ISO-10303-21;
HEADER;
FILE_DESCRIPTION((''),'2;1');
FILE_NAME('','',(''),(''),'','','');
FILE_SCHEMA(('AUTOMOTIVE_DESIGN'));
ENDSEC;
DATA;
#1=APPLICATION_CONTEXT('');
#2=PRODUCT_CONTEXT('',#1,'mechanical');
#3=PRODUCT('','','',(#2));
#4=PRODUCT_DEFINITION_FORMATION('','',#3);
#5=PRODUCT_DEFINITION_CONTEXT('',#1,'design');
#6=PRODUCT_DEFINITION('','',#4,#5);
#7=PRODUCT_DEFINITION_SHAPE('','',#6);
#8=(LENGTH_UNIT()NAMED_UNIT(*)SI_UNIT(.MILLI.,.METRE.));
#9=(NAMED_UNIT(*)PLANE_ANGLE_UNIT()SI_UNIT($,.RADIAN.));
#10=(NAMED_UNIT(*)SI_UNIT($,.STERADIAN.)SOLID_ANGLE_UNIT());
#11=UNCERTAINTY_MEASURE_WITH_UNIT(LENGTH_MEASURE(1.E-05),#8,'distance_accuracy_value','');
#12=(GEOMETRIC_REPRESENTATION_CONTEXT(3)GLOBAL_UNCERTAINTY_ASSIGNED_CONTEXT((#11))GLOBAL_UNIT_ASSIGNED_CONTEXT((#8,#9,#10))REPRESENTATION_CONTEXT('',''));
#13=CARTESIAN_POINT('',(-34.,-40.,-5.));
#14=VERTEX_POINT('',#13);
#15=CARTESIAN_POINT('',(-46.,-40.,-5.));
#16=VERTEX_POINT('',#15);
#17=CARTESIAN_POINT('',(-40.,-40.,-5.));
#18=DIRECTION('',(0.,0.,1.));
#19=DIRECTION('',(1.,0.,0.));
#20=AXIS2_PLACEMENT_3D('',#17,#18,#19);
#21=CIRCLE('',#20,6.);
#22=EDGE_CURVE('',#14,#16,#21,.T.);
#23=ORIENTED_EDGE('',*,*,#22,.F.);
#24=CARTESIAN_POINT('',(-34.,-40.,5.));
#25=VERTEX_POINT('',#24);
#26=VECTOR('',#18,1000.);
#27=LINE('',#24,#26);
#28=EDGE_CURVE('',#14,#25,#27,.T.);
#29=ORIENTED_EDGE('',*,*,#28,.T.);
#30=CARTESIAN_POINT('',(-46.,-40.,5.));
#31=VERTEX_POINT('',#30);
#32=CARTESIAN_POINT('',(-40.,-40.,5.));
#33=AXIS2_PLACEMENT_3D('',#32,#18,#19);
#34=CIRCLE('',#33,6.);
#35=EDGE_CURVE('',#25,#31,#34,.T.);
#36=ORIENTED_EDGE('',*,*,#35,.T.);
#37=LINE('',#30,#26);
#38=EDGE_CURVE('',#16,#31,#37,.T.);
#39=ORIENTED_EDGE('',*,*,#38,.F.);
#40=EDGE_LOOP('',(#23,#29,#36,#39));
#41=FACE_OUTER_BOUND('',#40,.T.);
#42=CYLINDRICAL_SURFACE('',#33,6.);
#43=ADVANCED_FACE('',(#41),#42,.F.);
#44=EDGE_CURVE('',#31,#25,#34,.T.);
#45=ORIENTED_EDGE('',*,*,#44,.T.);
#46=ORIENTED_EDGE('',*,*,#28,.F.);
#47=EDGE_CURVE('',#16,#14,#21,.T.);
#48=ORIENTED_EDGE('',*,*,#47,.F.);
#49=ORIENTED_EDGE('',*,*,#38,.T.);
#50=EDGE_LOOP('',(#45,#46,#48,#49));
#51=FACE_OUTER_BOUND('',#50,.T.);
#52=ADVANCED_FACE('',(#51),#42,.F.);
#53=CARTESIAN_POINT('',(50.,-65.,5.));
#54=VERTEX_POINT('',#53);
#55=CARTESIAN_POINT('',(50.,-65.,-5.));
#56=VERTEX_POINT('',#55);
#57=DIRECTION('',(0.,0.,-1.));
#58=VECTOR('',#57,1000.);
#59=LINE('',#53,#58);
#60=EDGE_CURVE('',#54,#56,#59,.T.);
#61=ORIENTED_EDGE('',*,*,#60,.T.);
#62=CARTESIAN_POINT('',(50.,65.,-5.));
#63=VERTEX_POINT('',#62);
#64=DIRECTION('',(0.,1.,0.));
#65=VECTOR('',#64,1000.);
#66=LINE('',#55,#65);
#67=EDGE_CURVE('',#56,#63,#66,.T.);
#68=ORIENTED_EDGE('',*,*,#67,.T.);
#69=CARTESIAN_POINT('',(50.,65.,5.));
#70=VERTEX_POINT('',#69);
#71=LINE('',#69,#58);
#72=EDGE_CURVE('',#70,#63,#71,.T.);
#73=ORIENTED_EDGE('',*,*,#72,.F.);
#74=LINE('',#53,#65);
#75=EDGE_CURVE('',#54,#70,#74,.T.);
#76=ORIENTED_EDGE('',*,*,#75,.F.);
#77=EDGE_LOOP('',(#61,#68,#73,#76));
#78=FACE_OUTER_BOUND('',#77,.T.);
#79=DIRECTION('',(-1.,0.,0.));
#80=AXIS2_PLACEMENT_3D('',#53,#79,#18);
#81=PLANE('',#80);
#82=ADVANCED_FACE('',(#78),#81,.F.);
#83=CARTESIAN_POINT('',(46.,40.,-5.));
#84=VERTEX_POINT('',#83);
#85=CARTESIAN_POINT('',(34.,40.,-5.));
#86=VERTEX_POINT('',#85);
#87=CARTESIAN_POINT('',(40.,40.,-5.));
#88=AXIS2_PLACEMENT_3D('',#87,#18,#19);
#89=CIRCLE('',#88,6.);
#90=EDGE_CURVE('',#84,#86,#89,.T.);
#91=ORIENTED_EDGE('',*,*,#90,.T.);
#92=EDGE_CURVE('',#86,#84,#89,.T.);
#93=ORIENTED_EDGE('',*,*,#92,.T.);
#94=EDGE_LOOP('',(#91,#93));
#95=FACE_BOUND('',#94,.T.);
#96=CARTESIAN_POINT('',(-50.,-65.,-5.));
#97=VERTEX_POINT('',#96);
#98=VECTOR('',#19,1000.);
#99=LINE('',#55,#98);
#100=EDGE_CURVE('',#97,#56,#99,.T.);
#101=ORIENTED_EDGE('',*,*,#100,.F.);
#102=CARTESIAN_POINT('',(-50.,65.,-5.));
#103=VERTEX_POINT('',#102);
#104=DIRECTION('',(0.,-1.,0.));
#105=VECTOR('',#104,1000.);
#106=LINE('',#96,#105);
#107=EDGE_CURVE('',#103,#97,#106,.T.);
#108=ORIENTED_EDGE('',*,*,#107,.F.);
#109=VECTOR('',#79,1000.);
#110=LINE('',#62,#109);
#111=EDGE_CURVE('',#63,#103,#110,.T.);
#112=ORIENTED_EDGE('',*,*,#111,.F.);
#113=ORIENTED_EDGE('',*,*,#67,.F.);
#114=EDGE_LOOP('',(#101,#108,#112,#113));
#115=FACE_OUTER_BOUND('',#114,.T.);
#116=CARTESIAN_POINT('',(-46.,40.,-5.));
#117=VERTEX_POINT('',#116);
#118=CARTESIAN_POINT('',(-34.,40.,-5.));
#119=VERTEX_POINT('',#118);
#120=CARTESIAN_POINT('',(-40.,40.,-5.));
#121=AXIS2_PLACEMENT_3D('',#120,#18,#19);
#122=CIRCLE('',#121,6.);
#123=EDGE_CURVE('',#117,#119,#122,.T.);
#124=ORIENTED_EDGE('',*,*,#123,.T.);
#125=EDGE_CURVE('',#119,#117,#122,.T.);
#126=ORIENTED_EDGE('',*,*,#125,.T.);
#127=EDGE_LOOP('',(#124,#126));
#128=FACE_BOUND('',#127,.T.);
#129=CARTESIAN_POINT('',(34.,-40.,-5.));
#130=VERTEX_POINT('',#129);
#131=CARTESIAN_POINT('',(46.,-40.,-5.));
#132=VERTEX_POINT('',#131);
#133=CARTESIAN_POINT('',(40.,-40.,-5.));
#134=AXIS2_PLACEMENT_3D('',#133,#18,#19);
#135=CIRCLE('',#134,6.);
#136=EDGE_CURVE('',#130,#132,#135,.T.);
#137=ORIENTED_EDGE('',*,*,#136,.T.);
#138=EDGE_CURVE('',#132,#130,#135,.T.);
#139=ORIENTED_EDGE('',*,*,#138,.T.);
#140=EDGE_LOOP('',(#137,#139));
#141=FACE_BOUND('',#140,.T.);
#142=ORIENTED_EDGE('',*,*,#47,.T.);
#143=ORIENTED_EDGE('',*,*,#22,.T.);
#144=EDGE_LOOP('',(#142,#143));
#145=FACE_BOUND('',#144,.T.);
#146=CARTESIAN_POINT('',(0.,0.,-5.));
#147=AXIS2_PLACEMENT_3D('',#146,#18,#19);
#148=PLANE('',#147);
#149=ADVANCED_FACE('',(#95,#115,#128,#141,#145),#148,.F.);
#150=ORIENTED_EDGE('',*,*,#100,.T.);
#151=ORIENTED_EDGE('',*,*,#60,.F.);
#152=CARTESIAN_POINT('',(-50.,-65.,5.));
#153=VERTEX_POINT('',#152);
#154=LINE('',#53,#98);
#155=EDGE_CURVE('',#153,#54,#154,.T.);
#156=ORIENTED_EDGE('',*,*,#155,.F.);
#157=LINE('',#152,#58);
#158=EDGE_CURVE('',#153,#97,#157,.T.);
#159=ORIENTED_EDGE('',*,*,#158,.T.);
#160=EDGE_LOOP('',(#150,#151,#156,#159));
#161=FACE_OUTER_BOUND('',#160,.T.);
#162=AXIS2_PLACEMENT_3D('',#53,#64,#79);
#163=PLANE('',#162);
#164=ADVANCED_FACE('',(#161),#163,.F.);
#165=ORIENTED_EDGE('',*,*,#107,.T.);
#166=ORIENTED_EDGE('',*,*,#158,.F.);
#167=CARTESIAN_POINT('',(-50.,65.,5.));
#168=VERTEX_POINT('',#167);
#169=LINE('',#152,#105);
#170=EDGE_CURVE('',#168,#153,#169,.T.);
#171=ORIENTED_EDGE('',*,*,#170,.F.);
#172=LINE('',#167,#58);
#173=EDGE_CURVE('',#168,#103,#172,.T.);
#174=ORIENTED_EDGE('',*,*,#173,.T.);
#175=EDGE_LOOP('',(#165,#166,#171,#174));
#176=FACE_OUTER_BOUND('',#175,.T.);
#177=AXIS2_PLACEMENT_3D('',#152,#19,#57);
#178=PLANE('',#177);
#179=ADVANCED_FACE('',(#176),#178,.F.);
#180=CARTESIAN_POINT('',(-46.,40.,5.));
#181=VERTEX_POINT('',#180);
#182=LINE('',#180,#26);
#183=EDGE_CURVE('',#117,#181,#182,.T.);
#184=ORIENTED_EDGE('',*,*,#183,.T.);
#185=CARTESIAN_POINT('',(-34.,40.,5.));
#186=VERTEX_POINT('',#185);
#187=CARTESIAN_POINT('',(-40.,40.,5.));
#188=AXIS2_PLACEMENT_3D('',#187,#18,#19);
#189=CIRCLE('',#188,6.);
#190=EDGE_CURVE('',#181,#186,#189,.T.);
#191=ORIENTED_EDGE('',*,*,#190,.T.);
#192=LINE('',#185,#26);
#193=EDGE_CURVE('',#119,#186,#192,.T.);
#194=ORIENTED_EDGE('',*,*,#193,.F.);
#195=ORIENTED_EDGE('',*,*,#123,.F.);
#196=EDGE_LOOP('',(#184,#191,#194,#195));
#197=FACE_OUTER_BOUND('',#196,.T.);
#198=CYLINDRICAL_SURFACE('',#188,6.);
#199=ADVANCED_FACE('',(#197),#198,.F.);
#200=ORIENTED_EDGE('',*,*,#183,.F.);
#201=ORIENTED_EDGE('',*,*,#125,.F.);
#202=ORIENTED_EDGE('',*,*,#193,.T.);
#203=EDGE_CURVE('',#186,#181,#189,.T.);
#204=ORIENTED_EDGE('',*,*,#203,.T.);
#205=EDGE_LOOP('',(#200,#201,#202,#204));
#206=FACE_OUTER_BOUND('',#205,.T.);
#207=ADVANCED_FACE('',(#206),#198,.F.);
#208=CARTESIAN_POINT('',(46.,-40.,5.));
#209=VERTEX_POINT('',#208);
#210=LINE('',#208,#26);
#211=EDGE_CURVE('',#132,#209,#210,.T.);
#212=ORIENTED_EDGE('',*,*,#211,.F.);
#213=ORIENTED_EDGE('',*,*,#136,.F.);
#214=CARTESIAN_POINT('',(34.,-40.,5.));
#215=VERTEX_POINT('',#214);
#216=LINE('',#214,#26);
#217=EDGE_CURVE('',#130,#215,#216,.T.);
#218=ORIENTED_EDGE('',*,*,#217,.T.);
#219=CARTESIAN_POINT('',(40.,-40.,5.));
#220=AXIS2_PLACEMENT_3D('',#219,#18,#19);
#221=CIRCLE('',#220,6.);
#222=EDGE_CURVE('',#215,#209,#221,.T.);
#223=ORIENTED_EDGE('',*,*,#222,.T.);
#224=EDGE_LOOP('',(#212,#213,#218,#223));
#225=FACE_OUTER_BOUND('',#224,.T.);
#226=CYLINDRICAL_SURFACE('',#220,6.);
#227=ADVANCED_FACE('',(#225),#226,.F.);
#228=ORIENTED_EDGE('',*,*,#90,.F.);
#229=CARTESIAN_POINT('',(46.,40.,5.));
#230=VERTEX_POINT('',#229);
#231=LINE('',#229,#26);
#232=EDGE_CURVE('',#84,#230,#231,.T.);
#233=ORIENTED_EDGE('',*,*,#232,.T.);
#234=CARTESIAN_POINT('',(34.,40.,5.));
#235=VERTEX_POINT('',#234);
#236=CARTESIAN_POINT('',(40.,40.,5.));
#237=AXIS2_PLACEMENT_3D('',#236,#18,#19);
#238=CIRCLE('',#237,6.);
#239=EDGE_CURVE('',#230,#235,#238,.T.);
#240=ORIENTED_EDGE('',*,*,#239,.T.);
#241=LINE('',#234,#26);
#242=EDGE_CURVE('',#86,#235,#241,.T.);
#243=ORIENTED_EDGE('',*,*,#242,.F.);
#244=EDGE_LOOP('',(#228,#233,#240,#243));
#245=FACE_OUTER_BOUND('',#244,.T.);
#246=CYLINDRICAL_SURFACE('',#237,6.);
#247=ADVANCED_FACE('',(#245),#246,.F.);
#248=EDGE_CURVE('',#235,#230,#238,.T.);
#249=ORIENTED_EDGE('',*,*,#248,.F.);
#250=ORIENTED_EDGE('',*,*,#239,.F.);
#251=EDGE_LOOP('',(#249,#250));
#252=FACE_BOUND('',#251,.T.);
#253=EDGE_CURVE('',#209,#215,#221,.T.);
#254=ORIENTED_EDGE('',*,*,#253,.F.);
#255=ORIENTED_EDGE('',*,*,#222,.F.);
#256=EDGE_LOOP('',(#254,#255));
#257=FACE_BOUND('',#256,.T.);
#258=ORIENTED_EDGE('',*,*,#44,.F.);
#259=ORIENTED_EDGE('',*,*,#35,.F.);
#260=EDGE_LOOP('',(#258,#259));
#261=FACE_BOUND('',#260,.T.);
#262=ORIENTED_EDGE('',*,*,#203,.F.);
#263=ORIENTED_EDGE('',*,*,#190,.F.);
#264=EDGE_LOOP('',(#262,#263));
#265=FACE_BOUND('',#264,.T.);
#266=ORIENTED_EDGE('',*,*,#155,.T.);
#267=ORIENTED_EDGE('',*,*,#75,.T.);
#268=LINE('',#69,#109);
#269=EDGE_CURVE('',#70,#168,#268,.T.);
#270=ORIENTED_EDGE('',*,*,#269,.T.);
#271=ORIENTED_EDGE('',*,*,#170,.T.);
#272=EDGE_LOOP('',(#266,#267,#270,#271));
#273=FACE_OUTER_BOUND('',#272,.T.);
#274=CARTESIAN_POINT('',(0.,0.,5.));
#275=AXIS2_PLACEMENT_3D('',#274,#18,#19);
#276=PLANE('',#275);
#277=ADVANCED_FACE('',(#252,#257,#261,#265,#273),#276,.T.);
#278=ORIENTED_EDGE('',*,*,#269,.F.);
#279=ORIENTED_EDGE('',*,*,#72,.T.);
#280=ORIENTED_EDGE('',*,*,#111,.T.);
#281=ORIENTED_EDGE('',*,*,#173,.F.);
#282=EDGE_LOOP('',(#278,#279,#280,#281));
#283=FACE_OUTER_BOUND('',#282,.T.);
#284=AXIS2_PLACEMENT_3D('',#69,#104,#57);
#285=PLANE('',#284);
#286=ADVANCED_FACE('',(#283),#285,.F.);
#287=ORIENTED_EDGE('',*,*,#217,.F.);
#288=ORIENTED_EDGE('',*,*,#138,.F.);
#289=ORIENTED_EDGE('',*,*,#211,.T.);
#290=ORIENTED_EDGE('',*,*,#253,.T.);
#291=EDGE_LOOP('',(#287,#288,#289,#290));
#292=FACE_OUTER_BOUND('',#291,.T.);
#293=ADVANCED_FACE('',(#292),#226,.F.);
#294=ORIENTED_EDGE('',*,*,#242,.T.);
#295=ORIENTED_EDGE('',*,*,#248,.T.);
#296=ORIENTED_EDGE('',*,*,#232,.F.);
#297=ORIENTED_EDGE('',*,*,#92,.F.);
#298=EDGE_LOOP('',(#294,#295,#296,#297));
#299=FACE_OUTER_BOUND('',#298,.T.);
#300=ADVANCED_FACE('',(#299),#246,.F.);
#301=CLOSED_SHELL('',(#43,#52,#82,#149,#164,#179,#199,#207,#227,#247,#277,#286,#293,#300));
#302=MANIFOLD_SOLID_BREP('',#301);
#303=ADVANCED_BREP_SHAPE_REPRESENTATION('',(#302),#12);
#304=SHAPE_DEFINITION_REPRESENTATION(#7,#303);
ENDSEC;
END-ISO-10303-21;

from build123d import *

# Parameters (mm, degrees)
SKETCH1_W           = 100
SKETCH1_H           = 130
BOSS_EXTRUDE1_DEPTH = 5
F_12_HOLE1_D        = 12


with BuildPart() as part:
    # Sketch1 → Boss-Extrude1 (new, symmetric)
    with BuildSketch(Plane.XY):
        Rectangle(SKETCH1_W, SKETCH1_H)
    extrude(amount=BOSS_EXTRUDE1_DEPTH, both=True)

    # Ø12 Hole1 (through all)
    with Locations(Plane.XY.offset(5)):
        with Locations((-40, 40), (40, 40), (40, -40), (-40, -40)):
            Hole(F_12_HOLE1_D / 2)


solid = part.part
